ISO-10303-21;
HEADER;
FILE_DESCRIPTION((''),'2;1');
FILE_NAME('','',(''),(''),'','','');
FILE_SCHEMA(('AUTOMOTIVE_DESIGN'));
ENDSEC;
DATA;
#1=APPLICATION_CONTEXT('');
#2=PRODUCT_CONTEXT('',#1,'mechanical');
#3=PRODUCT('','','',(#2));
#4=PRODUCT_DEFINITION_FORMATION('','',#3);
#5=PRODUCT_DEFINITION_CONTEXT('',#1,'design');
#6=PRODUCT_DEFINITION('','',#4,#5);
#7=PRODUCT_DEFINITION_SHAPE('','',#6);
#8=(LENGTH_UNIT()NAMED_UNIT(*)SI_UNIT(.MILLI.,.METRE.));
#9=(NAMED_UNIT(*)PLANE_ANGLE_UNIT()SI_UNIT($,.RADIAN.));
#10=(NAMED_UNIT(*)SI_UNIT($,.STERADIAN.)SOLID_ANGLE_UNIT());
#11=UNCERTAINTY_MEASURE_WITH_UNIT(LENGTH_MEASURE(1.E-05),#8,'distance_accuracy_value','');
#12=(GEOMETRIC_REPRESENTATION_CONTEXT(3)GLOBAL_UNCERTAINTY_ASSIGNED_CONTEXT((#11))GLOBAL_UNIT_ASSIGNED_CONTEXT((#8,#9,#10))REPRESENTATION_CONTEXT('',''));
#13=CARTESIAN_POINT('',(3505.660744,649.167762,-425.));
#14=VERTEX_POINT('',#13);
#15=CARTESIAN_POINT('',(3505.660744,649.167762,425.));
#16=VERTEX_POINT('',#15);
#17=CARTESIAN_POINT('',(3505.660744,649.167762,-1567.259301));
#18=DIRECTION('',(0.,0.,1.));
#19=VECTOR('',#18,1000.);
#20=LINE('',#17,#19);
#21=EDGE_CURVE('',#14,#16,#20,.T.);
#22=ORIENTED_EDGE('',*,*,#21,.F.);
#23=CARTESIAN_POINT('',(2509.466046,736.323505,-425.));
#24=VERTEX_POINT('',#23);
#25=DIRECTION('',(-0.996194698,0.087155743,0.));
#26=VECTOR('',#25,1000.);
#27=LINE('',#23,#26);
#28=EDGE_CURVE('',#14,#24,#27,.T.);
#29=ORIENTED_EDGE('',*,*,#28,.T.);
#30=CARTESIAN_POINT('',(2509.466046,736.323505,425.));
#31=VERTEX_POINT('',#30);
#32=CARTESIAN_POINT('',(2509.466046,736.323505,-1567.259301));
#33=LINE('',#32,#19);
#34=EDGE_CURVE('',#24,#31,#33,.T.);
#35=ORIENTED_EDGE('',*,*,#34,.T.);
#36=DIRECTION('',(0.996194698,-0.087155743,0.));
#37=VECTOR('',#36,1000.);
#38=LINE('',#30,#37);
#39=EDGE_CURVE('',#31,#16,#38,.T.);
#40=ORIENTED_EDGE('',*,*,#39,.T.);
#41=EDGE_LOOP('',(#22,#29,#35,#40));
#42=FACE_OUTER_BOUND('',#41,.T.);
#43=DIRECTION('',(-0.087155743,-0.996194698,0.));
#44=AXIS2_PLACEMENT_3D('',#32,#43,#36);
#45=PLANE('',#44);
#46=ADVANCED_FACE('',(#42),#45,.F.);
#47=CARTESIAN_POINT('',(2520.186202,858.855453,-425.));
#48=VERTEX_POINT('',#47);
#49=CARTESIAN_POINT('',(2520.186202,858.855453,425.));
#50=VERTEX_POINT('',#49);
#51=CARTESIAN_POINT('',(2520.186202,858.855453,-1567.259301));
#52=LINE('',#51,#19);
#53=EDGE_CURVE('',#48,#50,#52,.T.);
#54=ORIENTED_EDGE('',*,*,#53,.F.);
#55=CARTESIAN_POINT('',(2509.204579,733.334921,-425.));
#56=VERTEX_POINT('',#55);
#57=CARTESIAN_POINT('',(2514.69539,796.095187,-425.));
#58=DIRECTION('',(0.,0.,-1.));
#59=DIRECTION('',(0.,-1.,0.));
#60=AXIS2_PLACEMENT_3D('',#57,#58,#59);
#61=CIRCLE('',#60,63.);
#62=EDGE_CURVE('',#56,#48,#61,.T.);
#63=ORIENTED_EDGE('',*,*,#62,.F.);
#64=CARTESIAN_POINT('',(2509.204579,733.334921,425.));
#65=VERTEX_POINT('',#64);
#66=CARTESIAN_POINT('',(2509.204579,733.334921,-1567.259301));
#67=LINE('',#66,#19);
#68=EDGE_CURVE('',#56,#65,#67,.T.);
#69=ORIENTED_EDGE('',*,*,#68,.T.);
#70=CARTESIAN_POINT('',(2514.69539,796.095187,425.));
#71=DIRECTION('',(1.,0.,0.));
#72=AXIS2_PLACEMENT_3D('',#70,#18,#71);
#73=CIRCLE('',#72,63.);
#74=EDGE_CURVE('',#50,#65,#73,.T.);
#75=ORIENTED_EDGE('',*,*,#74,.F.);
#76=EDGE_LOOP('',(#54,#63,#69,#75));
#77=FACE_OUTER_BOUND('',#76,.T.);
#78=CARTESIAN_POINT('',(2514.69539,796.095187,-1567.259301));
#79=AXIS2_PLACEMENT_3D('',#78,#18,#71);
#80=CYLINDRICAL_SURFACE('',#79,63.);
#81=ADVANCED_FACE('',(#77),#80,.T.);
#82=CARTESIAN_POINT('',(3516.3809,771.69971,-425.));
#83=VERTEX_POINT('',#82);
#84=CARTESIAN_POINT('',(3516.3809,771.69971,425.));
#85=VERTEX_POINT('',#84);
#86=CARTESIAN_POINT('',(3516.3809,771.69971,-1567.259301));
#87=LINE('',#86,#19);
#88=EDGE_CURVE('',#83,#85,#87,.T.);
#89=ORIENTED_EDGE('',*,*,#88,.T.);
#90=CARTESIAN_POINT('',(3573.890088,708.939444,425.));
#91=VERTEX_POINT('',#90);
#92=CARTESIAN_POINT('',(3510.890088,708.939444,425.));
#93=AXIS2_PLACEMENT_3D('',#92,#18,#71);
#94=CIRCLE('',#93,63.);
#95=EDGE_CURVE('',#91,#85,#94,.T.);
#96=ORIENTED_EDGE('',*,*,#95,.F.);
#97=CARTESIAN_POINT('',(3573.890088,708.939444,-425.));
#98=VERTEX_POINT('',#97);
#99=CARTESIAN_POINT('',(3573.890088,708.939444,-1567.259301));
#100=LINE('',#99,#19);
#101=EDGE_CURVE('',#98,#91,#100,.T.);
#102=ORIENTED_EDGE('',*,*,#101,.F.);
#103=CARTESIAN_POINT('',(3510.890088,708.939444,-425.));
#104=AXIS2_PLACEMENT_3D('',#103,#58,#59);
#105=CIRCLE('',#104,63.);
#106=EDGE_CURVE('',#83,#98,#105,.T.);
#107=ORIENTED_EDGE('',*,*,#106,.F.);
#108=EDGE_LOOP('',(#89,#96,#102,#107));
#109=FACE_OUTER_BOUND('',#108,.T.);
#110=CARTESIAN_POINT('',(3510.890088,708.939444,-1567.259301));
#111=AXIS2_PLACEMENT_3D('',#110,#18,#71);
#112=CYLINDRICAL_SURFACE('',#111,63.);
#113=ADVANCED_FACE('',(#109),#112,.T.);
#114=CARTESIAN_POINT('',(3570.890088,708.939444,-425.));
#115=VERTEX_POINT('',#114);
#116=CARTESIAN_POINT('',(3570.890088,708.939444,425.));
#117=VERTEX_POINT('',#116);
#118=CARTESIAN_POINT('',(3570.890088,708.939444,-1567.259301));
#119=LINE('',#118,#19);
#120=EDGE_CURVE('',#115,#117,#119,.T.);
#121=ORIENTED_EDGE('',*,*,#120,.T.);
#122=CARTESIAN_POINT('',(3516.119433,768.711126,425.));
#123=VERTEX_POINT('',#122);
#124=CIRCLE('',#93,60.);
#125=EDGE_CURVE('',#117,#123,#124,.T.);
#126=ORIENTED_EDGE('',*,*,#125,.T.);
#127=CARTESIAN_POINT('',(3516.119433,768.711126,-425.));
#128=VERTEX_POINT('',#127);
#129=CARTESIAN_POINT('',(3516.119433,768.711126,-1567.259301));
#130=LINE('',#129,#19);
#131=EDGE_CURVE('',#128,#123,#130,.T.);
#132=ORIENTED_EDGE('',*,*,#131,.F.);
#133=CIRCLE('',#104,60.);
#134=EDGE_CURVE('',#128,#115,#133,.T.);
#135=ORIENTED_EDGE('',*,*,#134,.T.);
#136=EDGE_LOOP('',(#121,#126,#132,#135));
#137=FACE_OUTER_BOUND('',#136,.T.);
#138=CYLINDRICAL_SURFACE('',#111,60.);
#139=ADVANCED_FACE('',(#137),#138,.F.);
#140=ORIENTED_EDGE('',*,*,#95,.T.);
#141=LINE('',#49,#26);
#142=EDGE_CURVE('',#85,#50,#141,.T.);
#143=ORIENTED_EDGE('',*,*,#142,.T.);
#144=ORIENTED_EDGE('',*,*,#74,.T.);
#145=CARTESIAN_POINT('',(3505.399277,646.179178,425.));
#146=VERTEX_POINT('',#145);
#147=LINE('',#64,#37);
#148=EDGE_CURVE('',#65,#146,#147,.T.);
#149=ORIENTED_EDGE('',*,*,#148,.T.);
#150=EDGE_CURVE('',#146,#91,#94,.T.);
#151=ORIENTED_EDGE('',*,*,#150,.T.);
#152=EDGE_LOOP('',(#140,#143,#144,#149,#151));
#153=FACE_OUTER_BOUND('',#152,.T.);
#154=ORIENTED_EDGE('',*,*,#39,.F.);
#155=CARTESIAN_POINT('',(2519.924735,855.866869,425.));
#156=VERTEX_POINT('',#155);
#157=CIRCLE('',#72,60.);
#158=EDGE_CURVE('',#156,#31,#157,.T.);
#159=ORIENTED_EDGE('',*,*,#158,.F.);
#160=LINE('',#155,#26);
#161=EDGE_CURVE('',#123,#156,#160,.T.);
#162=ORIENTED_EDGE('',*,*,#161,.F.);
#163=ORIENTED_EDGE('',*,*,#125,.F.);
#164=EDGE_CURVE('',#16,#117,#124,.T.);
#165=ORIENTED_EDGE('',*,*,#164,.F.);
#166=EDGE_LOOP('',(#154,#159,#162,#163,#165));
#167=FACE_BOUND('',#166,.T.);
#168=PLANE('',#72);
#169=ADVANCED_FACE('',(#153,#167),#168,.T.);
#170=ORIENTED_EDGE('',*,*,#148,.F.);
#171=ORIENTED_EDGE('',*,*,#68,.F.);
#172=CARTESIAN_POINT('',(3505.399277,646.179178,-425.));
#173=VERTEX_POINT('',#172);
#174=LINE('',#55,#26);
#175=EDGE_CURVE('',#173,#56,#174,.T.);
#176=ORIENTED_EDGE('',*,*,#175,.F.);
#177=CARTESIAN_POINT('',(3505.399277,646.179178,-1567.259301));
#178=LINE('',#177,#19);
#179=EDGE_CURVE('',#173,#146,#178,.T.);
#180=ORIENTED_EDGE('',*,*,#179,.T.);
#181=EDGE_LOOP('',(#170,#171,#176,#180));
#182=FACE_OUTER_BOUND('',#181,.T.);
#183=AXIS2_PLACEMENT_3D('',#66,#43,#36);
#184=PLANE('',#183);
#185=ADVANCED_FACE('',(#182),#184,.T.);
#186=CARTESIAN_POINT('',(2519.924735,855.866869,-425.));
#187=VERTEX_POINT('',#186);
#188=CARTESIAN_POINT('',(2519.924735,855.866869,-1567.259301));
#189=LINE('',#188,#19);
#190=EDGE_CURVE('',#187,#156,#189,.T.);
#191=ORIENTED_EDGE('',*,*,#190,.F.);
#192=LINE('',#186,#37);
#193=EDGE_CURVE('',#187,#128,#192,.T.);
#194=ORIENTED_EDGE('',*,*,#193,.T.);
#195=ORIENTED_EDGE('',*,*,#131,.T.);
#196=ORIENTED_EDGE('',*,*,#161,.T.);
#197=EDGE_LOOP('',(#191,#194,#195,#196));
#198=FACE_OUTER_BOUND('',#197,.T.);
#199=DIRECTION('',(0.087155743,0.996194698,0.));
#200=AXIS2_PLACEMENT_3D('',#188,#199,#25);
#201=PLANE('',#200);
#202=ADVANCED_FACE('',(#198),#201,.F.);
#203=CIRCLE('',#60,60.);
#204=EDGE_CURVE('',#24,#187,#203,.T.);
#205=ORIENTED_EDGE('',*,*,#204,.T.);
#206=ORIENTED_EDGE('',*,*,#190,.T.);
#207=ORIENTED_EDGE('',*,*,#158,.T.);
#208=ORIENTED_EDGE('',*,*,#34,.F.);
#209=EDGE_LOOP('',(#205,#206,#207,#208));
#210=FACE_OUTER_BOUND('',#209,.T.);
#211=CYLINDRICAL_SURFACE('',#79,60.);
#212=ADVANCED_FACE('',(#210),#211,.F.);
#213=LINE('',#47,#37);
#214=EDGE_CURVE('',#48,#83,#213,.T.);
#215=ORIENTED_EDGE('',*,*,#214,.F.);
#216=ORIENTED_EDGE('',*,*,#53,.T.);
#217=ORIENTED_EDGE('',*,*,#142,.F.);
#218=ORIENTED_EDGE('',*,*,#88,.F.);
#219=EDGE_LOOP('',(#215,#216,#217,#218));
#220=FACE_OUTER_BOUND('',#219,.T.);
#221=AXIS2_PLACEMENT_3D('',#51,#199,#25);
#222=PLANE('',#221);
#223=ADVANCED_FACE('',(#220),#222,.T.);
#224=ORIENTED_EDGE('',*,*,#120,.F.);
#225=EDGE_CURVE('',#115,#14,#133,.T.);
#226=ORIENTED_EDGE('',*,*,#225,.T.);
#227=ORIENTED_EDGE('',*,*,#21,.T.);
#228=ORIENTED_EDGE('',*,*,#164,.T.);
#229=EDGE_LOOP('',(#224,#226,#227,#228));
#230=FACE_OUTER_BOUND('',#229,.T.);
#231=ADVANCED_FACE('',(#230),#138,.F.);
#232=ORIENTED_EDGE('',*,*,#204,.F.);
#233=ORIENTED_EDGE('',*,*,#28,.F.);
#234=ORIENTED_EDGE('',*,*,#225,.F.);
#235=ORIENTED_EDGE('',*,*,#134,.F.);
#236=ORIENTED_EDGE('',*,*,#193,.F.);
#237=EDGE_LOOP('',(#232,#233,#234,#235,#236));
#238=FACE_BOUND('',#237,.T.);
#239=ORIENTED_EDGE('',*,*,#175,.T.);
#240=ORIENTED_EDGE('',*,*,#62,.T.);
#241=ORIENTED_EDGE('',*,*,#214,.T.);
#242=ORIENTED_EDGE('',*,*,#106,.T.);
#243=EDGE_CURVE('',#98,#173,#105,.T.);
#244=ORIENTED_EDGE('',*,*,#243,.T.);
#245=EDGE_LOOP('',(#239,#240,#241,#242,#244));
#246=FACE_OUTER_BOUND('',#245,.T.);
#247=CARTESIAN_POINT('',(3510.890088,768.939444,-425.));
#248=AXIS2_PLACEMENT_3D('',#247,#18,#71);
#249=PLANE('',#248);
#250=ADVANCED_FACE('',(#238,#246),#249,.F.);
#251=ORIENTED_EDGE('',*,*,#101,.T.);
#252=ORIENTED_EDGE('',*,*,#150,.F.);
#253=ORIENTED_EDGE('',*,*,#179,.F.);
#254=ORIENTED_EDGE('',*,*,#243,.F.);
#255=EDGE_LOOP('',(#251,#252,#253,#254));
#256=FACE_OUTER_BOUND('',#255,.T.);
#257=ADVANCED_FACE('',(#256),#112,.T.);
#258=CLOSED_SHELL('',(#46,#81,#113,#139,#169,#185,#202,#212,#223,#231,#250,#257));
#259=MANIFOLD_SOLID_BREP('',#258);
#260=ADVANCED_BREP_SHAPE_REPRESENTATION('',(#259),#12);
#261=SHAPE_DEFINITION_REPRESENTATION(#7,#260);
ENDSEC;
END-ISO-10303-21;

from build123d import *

# Parameters (mm, degrees)
EXTRUDE_1_DEPTH = 850


with BuildPart() as part:
    # 草图1 → 凸台-拉伸1 (new body)
    with BuildSketch(Plane.XY.offset(425)):
        with BuildLine():
            Line((2520.186202106, 858.855453105), (3516.380900198, 771.699710358))
            ThreePointArc((3516.380900198, 771.699710358), (3573.650354384, 703.448632585), (3505.399276611, 646.179178398))
            Line((3505.399276611, 646.179178398), (2509.20457852, 733.334921146))
            ThreePointArc((2509.20457852, 733.334921146), (2451.935124333, 801.585998919), (2520.186202106, 858.855453105))
        make_face()
        with BuildLine():
            Line((2519.924734878, 855.866869011), (3516.119432969, 768.711126263))
            ThreePointArc((3516.119432969, 768.711126263), (3570.66177029, 703.710099813), (3505.66074384, 649.167762492))
            Line((3505.66074384, 649.167762492), (2509.466045748, 736.32350524))
            ThreePointArc((2509.466045748, 736.32350524), (2454.923708427, 801.32453169), (2519.924734878, 855.866869011))
        make_face(mode=Mode.SUBTRACT)
    extrude(amount=-EXTRUDE_1_DEPTH)


solid = part.part
